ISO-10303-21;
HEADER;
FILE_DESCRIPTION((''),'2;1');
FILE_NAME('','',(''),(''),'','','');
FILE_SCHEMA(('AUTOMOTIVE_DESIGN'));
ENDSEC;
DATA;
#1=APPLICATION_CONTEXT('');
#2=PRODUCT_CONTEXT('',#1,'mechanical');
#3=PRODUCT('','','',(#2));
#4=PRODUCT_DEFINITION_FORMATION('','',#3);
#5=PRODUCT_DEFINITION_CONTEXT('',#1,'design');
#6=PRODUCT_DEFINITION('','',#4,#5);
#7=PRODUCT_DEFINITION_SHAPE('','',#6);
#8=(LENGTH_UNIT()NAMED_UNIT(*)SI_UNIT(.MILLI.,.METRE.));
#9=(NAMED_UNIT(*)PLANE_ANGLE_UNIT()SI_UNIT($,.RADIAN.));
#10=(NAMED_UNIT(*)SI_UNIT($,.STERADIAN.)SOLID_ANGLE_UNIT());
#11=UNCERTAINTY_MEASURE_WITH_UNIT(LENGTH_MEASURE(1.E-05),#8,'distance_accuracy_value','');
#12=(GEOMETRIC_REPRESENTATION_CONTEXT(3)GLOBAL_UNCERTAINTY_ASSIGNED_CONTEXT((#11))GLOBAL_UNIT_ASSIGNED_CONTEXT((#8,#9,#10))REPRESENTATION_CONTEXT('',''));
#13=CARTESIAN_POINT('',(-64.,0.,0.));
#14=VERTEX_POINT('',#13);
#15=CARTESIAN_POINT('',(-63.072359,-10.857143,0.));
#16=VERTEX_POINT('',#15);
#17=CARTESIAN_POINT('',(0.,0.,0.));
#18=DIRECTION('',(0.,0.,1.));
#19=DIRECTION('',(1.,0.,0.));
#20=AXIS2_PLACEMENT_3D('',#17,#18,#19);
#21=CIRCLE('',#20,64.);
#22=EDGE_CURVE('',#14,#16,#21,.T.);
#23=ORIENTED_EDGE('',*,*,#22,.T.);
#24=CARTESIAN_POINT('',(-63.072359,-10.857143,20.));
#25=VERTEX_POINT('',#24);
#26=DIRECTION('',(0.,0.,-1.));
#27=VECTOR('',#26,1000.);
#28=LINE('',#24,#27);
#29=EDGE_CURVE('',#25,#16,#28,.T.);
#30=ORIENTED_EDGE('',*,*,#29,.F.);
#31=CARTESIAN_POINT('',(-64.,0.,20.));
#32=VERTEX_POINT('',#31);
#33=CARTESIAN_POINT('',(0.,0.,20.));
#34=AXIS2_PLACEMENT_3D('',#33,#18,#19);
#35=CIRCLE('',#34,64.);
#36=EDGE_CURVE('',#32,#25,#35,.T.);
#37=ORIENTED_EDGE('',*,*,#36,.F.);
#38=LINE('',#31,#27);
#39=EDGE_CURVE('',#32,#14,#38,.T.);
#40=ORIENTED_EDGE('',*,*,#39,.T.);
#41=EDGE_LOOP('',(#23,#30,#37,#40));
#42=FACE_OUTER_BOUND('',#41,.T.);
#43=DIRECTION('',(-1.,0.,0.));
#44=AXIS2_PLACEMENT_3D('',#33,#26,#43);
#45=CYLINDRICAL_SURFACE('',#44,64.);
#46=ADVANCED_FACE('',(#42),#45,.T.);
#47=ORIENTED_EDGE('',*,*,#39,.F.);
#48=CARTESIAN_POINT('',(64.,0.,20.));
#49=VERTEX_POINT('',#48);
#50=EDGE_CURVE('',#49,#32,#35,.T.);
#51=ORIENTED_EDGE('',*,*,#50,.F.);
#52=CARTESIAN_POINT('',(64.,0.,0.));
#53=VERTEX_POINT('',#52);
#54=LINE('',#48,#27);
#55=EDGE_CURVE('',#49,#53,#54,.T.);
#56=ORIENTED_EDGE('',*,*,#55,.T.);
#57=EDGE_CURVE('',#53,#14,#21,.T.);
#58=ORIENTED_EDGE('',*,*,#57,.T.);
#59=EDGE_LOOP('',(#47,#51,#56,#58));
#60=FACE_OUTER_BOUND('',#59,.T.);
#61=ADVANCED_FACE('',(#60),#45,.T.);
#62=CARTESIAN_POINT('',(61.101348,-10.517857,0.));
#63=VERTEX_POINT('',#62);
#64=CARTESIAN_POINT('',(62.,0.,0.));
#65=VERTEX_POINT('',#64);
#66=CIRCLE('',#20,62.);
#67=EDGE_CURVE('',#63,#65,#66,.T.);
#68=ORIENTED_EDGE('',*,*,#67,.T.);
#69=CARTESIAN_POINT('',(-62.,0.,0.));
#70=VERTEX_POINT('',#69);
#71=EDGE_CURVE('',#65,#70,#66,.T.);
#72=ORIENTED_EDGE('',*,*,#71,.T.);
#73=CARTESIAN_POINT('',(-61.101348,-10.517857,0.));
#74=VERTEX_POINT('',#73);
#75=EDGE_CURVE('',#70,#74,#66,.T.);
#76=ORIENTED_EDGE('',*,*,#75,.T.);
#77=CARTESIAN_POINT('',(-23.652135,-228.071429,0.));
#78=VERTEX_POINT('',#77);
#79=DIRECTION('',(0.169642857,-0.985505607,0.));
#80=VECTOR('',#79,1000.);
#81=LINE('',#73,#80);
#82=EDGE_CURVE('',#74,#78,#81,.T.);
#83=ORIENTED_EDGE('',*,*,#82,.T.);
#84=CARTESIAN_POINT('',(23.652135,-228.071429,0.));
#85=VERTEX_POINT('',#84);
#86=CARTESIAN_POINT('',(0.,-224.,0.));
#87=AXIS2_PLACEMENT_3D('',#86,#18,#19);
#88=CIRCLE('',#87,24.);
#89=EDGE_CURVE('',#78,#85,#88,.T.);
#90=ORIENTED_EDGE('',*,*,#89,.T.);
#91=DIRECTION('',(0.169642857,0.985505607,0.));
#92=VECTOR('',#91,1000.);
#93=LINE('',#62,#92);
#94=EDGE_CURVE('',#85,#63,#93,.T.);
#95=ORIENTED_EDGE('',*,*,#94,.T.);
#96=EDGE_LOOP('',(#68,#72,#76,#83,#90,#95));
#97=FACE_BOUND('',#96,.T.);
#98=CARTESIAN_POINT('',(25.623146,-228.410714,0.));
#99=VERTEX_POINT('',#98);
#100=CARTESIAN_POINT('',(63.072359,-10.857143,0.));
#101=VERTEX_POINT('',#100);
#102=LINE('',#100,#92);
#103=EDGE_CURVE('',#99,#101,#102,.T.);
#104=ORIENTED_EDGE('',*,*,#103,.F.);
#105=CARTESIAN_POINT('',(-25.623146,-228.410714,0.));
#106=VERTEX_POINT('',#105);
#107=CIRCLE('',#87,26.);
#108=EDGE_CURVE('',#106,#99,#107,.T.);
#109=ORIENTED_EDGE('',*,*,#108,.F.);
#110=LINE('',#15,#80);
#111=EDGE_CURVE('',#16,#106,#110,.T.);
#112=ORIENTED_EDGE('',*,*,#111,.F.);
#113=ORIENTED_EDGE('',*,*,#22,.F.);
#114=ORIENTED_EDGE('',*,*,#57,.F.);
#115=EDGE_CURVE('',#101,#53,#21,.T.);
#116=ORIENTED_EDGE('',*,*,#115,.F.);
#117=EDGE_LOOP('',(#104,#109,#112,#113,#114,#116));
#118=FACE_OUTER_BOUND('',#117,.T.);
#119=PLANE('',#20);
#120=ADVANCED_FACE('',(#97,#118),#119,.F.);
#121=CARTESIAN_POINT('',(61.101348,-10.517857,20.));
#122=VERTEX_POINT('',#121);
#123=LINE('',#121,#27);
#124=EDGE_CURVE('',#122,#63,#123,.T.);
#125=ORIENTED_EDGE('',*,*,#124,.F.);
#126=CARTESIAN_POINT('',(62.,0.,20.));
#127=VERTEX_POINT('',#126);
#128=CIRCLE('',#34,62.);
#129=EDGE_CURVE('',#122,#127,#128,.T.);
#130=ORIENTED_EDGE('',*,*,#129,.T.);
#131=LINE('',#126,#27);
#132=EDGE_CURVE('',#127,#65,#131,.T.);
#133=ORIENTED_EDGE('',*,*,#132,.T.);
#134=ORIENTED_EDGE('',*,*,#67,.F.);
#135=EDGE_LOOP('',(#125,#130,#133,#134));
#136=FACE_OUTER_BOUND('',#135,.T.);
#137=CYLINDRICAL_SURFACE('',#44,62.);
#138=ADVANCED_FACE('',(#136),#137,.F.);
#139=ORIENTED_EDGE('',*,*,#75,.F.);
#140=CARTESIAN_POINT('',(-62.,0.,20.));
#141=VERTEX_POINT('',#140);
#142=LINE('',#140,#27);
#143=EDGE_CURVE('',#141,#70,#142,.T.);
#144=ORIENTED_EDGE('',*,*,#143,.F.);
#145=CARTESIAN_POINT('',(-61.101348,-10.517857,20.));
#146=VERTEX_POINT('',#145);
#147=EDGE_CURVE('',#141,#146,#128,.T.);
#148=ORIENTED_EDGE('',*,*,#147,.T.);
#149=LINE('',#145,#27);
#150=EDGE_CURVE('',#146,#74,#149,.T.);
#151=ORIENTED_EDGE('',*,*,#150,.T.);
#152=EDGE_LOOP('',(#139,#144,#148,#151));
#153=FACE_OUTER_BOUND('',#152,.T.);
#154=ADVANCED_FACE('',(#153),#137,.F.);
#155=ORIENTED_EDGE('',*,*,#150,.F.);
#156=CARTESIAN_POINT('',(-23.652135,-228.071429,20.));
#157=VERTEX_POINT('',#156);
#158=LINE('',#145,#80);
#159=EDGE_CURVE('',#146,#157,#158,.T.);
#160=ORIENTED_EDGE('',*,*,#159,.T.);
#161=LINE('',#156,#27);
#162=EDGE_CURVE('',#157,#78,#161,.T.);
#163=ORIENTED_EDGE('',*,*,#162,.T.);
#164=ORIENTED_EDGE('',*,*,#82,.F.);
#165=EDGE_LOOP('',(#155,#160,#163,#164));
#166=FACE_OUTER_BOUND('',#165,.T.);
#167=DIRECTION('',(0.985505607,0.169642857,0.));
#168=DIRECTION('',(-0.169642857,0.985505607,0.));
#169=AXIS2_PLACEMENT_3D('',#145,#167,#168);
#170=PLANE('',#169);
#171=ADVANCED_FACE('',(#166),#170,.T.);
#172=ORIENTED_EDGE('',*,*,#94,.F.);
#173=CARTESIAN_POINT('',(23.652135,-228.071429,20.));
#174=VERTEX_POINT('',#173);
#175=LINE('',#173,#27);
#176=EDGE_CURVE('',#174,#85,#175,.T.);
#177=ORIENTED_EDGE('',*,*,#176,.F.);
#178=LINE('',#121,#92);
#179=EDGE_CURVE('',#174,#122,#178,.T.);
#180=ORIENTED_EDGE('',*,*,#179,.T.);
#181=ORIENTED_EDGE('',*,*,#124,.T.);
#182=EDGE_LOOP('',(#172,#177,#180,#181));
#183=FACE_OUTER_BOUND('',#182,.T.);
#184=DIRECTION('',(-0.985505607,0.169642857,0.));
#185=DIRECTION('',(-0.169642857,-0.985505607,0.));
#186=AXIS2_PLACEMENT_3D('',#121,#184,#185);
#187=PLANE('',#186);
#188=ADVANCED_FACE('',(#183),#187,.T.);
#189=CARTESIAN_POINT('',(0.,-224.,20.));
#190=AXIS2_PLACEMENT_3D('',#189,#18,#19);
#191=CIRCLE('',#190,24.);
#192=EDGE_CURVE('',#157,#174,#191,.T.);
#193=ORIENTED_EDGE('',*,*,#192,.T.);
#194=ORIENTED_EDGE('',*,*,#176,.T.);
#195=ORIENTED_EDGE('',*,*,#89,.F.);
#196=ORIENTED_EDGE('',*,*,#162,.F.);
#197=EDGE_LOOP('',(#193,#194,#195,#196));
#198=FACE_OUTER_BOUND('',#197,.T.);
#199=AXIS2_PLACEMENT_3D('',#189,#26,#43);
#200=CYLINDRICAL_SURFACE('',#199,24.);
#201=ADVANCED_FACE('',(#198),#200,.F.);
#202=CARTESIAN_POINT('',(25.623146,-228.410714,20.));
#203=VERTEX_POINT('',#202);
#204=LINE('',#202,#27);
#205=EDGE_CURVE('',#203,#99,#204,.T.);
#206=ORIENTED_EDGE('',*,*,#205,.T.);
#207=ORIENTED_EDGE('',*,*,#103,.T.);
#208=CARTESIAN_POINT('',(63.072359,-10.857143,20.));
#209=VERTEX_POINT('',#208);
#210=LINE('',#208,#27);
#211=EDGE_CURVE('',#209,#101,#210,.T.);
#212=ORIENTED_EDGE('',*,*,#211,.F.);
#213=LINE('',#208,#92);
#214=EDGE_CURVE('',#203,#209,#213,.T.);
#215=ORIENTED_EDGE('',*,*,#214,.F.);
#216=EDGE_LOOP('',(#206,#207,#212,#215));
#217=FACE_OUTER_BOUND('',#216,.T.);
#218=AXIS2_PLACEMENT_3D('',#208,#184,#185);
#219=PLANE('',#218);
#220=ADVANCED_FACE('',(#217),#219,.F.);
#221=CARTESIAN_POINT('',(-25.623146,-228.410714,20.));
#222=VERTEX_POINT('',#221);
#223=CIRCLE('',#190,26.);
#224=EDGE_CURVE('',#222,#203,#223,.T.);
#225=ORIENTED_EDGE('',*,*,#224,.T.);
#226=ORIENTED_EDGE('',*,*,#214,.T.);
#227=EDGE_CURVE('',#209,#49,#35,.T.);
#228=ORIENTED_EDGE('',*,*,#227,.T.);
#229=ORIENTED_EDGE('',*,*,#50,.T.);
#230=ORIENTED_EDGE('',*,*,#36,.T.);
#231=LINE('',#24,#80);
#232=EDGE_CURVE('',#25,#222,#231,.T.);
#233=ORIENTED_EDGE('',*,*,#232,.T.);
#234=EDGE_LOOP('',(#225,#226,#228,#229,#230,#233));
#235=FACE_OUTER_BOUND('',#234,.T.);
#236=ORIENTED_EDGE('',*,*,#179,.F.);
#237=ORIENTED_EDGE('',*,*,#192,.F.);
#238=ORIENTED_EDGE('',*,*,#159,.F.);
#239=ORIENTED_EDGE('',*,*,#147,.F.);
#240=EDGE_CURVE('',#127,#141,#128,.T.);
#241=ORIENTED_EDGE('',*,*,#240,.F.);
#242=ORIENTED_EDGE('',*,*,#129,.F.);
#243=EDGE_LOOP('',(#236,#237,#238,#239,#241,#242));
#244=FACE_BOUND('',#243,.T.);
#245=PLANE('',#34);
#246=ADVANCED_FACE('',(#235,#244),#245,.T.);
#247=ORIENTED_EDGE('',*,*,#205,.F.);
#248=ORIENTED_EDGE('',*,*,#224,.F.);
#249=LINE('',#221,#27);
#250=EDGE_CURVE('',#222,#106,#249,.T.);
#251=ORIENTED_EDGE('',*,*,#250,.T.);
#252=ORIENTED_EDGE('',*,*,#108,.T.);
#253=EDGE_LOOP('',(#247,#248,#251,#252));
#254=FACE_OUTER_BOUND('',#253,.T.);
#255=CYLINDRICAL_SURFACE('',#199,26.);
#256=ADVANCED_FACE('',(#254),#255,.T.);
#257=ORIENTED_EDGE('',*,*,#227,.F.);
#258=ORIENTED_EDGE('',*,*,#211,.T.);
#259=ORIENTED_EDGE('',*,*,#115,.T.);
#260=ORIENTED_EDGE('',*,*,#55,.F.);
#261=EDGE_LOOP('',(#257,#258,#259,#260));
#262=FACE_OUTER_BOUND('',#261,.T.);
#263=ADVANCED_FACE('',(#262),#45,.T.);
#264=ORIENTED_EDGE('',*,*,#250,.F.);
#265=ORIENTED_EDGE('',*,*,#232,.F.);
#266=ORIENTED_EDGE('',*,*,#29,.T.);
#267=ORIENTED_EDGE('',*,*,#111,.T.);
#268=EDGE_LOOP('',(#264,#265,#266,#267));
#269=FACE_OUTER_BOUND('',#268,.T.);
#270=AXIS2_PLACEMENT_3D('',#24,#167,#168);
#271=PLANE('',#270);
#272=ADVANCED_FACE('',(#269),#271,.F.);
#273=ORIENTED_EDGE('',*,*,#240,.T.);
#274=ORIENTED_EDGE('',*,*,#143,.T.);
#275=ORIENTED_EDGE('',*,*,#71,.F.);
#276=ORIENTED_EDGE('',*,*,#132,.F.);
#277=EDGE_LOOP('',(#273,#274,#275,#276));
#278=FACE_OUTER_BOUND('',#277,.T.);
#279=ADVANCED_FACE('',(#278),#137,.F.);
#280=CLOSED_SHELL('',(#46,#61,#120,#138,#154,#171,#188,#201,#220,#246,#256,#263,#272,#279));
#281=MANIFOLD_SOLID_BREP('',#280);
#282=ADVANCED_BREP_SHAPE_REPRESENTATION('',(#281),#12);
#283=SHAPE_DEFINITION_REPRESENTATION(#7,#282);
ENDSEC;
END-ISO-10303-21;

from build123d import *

# Parameters (mm, degrees)
EXTRUDE_1_DEPTH = 20


with BuildPart() as part:
    # 草图1 → 拉伸-薄壁1 (new body)
    with BuildSketch(Plane.XY):
        with BuildLine():
            Line((25.623145777, -228.410714286), (63.072358835, -10.857142857))
            ThreePointArc((63.072358835, -10.857142857), (0, 64), (-63.072358835, -10.857142857))
            Line((-63.072358835, -10.857142857), (-25.623145777, -228.410714286))
            ThreePointArc((-25.623145777, -228.410714286), (0, -250), (25.623145777, -228.410714286))
        make_face()
        with BuildLine():
            Line((23.652134563, -228.071428571), (61.101347621, -10.517857143))
            ThreePointArc((61.101347621, -10.517857143), (0, 62), (-61.101347621, -10.517857143))
            Line((-61.101347621, -10.517857143), (-23.652134563, -228.071428571))
            ThreePointArc((-23.652134563, -228.071428571), (0, -248), (23.652134563, -228.071428571))
        make_face(mode=Mode.SUBTRACT)
    extrude(amount=EXTRUDE_1_DEPTH)


solid = part.part
